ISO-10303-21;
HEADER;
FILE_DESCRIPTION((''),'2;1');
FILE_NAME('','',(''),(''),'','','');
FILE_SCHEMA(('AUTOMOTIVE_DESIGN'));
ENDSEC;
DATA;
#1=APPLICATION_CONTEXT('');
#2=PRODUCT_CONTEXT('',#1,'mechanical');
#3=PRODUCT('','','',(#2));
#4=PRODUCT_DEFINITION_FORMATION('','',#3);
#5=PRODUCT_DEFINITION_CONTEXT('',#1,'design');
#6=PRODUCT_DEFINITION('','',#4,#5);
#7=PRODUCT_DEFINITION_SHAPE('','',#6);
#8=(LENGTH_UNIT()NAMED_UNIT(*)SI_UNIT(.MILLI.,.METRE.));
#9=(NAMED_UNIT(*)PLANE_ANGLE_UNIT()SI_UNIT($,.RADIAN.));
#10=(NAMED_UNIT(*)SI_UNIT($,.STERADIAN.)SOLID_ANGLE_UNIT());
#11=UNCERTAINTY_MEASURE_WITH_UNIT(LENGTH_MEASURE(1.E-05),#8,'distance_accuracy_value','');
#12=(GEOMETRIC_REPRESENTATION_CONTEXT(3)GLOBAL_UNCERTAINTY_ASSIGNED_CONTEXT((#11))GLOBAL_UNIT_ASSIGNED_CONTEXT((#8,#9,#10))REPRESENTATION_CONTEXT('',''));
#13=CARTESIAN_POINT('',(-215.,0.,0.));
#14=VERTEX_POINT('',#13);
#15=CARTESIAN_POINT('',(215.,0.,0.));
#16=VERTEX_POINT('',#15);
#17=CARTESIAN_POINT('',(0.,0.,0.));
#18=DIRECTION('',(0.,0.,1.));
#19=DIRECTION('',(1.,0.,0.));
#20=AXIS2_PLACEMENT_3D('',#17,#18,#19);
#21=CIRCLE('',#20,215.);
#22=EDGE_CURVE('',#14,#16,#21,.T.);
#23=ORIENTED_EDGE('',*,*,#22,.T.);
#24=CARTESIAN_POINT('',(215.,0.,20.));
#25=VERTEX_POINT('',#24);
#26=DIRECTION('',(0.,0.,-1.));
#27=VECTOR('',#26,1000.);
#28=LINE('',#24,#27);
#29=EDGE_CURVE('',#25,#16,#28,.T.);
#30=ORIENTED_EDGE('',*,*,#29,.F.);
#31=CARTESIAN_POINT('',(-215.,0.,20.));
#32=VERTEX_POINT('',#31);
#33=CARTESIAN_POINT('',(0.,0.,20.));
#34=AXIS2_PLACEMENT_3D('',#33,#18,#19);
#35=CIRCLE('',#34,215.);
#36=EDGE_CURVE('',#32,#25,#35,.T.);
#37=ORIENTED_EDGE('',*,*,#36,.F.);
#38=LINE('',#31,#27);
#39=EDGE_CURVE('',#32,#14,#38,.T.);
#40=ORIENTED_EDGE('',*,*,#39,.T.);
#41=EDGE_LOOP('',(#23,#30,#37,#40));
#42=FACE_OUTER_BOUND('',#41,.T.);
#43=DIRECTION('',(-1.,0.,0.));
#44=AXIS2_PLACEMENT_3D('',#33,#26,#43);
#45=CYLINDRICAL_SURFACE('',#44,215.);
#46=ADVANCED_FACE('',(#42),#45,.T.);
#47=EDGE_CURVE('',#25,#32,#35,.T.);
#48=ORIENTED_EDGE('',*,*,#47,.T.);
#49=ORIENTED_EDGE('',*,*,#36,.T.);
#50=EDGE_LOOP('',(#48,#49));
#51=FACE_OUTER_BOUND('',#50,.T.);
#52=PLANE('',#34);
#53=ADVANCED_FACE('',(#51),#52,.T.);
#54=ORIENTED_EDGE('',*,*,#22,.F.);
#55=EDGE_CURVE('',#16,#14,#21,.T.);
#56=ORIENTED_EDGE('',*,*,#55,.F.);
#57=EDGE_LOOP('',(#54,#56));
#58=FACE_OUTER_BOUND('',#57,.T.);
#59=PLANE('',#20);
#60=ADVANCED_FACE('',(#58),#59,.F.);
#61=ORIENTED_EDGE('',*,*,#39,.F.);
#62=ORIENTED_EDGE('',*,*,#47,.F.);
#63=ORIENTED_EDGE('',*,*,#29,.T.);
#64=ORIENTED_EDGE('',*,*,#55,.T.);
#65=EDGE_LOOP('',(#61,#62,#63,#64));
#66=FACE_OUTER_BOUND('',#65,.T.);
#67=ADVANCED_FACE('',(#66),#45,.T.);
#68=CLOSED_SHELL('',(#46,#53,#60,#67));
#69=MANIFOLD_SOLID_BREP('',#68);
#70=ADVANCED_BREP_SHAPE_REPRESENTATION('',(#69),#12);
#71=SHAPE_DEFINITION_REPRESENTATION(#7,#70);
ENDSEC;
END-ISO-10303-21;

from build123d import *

# Parameters (mm, degrees)
SKETCH1_R           = 215
BOSS_EXTRUDE1_DEPTH = 20


with BuildPart() as part:
    # Sketch1 → Boss-Extrude1 (new body)
    with BuildSketch(Plane.XY):
        Circle(SKETCH1_R)
    extrude(amount=BOSS_EXTRUDE1_DEPTH)


solid = part.part
